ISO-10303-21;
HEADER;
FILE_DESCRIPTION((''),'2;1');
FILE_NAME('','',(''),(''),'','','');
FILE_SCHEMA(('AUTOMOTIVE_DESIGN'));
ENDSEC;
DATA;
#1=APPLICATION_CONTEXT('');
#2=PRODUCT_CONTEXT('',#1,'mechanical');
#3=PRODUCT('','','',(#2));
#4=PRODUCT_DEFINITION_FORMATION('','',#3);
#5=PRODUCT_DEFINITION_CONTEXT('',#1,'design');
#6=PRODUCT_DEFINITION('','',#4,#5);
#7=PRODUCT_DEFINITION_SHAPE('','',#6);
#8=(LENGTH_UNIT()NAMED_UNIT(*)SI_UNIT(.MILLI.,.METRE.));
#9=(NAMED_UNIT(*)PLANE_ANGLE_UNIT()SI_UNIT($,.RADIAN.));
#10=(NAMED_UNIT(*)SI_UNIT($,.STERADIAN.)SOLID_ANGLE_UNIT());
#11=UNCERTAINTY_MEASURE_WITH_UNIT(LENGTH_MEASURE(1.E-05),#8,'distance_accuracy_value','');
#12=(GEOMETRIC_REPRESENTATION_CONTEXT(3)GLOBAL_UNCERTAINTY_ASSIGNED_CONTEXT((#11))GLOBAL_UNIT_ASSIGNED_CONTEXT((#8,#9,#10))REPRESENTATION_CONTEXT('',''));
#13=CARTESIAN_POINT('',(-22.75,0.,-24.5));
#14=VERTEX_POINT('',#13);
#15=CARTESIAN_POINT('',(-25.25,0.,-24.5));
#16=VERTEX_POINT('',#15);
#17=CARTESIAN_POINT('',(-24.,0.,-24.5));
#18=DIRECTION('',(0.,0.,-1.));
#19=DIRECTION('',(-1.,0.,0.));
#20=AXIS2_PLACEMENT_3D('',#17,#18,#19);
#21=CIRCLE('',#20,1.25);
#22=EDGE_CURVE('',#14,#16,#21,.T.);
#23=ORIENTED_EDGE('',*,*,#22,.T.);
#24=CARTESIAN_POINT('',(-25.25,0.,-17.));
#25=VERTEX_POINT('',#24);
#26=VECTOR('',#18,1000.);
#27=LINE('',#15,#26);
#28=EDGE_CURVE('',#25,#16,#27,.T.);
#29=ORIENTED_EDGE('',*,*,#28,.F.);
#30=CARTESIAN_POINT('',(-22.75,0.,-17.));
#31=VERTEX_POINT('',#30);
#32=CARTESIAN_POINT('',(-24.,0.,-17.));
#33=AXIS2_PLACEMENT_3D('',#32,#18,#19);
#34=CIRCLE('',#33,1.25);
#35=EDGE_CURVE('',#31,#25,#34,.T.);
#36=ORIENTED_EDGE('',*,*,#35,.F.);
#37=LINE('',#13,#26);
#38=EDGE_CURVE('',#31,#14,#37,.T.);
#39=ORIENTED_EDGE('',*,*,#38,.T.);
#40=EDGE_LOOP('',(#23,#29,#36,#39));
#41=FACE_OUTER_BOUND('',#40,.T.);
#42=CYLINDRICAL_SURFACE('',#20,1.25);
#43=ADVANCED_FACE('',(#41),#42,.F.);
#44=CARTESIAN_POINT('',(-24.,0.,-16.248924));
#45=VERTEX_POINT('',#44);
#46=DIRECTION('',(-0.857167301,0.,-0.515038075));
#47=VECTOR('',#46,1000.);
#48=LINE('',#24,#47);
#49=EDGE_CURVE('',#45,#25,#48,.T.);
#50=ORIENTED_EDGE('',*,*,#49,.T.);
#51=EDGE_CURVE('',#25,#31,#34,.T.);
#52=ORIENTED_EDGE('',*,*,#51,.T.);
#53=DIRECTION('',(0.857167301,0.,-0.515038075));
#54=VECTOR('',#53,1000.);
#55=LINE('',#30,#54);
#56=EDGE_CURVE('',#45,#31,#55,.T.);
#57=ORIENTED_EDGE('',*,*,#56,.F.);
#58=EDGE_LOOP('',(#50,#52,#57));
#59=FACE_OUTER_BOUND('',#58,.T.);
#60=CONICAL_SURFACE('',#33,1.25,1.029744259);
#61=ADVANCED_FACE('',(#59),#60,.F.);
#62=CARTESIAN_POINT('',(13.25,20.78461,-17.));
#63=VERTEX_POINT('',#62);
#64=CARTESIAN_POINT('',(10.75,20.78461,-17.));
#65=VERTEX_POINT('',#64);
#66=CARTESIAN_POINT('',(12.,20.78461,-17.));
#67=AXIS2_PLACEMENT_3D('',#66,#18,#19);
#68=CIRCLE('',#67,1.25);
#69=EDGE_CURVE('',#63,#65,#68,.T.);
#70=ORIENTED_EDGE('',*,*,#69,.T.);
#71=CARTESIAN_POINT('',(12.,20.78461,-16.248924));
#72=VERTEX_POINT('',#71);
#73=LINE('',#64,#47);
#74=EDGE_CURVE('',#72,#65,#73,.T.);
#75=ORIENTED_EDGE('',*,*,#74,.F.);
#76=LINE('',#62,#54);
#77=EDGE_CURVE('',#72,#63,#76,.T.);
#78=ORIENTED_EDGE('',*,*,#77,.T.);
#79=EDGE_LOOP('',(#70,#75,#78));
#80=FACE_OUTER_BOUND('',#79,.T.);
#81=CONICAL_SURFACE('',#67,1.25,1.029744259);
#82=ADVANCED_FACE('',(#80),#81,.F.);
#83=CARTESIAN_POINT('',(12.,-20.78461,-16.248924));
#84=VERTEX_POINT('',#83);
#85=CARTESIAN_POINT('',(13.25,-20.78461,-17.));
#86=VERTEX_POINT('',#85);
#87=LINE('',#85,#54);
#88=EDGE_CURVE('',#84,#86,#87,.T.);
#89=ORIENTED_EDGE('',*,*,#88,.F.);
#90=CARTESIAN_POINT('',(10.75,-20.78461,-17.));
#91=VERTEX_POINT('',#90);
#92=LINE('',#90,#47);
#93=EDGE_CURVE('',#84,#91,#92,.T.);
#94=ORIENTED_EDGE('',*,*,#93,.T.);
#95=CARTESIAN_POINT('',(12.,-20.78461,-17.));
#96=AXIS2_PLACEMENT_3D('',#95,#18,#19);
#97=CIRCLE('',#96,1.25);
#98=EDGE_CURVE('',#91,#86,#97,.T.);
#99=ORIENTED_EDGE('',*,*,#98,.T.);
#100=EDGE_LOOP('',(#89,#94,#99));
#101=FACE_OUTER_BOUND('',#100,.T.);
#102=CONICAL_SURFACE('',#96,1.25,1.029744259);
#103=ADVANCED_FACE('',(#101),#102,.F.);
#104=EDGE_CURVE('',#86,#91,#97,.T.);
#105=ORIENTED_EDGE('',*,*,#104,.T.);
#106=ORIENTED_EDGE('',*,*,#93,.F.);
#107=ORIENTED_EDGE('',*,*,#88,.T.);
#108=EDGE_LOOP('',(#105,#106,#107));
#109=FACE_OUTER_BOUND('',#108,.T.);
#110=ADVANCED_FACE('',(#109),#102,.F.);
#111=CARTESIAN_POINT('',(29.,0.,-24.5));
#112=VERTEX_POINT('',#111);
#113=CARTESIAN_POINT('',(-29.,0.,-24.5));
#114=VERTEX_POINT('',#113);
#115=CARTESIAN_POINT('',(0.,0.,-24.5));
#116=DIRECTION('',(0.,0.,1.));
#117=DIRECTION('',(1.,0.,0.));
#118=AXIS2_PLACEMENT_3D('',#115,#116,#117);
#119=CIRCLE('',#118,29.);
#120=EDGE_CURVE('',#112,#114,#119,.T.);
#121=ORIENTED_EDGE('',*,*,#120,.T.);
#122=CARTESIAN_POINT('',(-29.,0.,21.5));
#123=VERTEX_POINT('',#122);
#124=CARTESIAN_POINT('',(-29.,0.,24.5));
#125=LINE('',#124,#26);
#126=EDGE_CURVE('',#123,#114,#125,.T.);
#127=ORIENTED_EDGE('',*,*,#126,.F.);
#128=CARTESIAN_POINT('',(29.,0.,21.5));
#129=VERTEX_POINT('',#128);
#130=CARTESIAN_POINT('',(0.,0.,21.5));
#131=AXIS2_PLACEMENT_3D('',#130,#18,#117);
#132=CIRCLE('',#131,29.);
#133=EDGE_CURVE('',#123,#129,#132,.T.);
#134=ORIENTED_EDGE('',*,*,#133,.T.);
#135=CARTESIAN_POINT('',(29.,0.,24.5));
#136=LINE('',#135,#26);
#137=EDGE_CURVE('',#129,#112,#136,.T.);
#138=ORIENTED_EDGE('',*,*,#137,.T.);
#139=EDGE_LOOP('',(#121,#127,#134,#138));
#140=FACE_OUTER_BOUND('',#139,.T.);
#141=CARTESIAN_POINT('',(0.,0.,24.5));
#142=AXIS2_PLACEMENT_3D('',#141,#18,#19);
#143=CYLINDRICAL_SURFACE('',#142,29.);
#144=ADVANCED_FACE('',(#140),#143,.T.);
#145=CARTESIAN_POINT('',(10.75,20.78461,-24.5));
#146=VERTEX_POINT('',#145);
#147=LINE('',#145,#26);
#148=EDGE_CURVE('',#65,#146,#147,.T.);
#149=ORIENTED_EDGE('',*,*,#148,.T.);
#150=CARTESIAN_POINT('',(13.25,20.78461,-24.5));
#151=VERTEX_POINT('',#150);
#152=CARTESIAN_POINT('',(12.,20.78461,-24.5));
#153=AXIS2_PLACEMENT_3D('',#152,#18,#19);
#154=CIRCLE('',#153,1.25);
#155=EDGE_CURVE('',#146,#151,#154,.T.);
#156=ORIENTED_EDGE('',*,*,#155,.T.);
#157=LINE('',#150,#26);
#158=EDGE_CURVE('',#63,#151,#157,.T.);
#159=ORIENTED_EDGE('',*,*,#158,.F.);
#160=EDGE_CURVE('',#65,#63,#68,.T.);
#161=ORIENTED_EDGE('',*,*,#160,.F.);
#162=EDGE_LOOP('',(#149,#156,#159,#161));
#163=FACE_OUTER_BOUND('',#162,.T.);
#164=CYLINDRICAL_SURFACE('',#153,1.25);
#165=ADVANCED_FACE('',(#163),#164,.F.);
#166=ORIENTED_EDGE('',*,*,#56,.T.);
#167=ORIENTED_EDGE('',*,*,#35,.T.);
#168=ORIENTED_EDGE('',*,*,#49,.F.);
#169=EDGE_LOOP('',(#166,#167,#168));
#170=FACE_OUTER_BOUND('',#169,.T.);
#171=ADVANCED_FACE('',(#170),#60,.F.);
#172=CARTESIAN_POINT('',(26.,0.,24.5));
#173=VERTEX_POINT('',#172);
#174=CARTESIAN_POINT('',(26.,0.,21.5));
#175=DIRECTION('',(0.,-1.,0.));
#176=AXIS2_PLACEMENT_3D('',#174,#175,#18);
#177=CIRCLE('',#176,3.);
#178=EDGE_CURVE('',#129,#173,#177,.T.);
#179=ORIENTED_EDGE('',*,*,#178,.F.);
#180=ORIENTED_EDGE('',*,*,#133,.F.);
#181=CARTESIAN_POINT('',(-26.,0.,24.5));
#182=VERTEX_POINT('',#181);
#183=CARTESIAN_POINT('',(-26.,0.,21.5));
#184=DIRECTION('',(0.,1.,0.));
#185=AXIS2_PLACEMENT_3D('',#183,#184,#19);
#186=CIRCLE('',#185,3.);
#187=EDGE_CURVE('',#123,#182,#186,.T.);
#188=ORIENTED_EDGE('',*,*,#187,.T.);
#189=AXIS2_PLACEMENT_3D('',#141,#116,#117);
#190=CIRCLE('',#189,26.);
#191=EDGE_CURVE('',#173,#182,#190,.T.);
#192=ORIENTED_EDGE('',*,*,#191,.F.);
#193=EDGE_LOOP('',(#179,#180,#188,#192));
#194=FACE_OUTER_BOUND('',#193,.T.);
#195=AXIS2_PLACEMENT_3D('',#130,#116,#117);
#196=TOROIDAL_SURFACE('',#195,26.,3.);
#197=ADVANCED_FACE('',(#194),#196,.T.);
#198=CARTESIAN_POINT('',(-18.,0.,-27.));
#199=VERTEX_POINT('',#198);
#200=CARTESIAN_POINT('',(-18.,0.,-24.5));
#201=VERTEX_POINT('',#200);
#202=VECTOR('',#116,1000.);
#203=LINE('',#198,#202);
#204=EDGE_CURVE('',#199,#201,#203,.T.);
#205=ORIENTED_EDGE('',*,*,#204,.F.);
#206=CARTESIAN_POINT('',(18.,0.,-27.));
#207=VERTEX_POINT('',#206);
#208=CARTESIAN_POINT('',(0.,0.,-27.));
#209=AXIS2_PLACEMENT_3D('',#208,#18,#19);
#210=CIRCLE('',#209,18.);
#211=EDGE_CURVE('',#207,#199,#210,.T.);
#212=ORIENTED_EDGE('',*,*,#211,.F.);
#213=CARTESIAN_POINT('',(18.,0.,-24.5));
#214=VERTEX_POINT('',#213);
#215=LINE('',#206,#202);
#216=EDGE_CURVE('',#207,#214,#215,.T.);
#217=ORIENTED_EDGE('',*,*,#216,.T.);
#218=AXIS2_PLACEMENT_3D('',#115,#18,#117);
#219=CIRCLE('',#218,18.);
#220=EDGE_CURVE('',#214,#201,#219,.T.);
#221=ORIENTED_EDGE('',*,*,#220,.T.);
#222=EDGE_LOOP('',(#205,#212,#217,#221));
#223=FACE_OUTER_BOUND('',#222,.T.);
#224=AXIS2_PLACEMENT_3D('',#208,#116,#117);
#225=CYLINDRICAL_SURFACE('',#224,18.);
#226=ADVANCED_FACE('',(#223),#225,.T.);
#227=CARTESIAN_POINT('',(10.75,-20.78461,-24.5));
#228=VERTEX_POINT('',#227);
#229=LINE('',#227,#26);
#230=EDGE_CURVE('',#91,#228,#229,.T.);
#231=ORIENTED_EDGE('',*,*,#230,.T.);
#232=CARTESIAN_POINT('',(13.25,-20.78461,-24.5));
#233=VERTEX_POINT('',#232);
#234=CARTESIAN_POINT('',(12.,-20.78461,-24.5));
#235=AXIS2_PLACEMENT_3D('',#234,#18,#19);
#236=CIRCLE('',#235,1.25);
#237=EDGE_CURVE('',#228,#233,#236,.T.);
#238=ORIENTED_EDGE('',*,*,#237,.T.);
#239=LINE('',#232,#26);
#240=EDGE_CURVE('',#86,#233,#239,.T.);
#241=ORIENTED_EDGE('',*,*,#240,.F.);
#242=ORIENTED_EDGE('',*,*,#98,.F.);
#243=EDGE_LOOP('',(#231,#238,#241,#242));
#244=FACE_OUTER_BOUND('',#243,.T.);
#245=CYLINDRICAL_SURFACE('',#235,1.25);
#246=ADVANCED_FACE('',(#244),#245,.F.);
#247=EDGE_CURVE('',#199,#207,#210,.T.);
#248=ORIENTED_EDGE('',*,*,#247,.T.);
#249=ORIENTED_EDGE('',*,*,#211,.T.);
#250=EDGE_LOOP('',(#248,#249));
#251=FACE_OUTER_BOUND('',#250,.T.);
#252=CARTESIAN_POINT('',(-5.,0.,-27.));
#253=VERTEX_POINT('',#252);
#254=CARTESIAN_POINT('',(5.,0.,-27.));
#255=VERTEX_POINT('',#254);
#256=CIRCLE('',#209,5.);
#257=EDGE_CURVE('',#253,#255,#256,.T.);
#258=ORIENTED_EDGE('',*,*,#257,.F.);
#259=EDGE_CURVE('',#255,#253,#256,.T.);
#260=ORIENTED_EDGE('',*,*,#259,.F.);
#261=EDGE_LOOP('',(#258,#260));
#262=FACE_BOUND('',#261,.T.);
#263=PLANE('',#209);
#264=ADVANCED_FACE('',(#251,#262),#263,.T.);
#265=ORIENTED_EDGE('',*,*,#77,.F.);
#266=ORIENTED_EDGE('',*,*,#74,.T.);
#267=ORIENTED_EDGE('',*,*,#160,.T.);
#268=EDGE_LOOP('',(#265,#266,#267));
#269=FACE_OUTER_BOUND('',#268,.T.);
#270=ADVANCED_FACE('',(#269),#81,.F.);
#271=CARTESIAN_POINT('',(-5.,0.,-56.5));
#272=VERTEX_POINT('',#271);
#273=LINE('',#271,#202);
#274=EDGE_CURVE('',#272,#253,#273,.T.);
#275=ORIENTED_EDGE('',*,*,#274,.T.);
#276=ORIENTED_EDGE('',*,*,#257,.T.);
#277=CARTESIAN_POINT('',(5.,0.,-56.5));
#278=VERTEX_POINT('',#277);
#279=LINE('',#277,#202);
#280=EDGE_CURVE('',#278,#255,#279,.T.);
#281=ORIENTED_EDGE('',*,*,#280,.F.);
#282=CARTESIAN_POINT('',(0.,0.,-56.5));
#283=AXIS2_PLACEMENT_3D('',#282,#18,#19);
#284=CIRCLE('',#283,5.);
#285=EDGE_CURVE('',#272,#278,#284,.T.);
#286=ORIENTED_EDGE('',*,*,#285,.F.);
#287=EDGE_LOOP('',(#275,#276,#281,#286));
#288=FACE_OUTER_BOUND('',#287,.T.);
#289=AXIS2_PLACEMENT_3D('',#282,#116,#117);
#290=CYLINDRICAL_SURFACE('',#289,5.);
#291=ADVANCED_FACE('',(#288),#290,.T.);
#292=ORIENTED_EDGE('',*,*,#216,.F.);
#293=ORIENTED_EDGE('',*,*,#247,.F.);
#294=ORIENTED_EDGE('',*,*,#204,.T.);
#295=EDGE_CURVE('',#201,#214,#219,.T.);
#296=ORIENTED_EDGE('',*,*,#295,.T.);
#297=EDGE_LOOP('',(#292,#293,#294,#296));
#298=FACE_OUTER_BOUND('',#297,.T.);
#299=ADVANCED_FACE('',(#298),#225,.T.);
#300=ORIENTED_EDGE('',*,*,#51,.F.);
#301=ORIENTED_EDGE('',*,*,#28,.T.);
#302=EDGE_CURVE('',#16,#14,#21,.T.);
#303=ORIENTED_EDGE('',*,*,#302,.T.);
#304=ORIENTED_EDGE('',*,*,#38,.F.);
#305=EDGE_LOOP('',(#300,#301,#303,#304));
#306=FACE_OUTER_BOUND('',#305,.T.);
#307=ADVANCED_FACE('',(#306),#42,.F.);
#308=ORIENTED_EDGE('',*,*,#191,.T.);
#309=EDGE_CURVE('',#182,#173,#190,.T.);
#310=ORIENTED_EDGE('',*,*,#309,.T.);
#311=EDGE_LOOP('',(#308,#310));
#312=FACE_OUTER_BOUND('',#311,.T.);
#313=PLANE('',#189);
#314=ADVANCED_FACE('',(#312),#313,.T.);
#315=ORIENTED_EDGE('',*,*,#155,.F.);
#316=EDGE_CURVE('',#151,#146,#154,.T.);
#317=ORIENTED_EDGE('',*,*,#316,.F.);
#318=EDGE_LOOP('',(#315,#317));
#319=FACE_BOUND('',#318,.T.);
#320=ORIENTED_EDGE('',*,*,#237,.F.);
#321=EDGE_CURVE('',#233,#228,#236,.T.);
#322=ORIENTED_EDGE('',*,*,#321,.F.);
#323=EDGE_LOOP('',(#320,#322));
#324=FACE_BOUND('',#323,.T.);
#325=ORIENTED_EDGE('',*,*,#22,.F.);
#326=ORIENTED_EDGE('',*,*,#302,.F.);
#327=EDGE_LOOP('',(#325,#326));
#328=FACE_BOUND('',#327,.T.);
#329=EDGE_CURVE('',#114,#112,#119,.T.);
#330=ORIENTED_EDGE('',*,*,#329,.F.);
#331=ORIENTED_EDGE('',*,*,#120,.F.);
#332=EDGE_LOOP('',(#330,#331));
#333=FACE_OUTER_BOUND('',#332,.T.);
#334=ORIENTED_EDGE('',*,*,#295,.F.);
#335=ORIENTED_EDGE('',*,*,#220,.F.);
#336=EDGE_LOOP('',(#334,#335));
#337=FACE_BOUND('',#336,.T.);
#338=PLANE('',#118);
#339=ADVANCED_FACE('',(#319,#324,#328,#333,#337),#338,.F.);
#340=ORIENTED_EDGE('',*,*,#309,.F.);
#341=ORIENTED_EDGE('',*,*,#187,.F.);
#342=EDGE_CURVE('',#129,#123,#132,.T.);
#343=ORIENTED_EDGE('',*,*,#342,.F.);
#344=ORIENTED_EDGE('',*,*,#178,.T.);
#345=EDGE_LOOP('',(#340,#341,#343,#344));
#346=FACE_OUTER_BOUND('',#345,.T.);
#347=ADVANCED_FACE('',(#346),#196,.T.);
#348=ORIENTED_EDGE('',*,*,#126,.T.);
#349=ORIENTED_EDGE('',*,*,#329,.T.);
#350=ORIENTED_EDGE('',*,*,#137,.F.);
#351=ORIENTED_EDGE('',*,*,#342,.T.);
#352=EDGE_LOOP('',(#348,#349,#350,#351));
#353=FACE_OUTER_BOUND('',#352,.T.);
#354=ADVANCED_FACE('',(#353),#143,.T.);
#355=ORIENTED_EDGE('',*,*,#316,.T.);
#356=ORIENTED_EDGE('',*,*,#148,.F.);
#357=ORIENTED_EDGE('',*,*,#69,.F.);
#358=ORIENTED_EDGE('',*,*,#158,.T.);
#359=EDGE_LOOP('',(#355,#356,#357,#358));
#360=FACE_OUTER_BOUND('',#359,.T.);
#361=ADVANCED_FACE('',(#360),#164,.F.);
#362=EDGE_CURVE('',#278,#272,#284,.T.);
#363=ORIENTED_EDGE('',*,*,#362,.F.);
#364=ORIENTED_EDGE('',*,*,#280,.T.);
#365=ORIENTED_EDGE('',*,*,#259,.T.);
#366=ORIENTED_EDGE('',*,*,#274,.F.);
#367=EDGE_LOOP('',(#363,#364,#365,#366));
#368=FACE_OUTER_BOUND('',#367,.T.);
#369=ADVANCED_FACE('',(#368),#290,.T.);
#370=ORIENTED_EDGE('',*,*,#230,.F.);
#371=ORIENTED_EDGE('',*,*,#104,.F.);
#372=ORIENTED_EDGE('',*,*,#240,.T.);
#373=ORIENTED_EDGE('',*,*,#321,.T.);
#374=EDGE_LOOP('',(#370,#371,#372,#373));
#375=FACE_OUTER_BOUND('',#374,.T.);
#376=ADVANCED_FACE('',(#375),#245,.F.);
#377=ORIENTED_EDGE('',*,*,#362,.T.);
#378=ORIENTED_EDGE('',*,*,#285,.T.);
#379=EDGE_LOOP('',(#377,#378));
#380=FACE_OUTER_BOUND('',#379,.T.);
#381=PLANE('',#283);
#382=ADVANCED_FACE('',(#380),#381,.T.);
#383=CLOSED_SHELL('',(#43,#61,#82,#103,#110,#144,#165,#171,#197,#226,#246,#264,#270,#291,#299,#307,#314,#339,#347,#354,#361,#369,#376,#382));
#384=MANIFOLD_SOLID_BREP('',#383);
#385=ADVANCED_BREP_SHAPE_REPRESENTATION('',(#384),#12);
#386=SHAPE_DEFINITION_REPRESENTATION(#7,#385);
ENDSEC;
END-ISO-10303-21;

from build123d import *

# Parameters (mm, degrees)
SKETCH_1_R               = 29
EXTRUDE_1_DEPTH          = 24.5
FILLET_1_R               = 3
SKETCH_2_R               = 5
EXTRUDE_2_DEPTH          = 32
PATTERN_CIRCULAR_1_COUNT = 3
SKETCH_5_R               = 18
EXTRUDE_3_DEPTH          = 2.5


with BuildPart() as part:
    # 草图1 → 凸台-拉伸1 (new, symmetric)
    with BuildSketch(Plane.XY):
        Circle(SKETCH_1_R)
    extrude(amount=EXTRUDE_1_DEPTH, both=True)

    # 圆角1
    fillet_1_edges = [part.edges().sort_by_distance(p)[0] for p in [
        (-29, 0, 24.5),
    ]]
    fillet(fillet_1_edges, radius=FILLET_1_R)

    # 草图2 → 凸台-拉伸2 (add)
    with BuildSketch(Plane(origin=(0, 0, -24.5), x_dir=(-1, 0, 0), z_dir=(0, 0, -1))):
        with Locations(Location((0, 0, 0), (0, 0, 180))):
            Circle(SKETCH_2_R)
    extrude(amount=EXTRUDE_2_DEPTH)

    # 草图3 → M3 螺纹孔1 (revolve, cut)
    with BuildSketch(Plane(origin=(-24, 0, -24.5), x_dir=(0, 1, 0), z_dir=(1, 0, 0))):
        Polygon((0, 0), (0, 8.251075774), (1.25, 7.5), (1.25, 0), align=None)
    hole_wizard_m3_1 = revolve(axis=Axis((-24, 0, -30.85), (0, 0, 1)), mode=Mode.SUBTRACT)

    # 阵列(圆周)1: M3 螺纹孔1 ×3 about axis
    pattern_circular_1_axis = Axis((0, 0, 0), (0, 0, 1))
    for i in range(1, PATTERN_CIRCULAR_1_COUNT):
        add(hole_wizard_m3_1.rotate(pattern_circular_1_axis, i * 360 / PATTERN_CIRCULAR_1_COUNT), mode=Mode.SUBTRACT)

    # 草图5 → 凸台-拉伸3 (add)
    with BuildSketch(Plane(origin=(0, 0, -24.5), x_dir=(-1, 0, 0), z_dir=(0, 0, -1))):
        with Locations(Location((0, 0, 0), (0, 0, 180))):
            Circle(SKETCH_5_R)
    extrude(amount=EXTRUDE_3_DEPTH)


solid = part.part
